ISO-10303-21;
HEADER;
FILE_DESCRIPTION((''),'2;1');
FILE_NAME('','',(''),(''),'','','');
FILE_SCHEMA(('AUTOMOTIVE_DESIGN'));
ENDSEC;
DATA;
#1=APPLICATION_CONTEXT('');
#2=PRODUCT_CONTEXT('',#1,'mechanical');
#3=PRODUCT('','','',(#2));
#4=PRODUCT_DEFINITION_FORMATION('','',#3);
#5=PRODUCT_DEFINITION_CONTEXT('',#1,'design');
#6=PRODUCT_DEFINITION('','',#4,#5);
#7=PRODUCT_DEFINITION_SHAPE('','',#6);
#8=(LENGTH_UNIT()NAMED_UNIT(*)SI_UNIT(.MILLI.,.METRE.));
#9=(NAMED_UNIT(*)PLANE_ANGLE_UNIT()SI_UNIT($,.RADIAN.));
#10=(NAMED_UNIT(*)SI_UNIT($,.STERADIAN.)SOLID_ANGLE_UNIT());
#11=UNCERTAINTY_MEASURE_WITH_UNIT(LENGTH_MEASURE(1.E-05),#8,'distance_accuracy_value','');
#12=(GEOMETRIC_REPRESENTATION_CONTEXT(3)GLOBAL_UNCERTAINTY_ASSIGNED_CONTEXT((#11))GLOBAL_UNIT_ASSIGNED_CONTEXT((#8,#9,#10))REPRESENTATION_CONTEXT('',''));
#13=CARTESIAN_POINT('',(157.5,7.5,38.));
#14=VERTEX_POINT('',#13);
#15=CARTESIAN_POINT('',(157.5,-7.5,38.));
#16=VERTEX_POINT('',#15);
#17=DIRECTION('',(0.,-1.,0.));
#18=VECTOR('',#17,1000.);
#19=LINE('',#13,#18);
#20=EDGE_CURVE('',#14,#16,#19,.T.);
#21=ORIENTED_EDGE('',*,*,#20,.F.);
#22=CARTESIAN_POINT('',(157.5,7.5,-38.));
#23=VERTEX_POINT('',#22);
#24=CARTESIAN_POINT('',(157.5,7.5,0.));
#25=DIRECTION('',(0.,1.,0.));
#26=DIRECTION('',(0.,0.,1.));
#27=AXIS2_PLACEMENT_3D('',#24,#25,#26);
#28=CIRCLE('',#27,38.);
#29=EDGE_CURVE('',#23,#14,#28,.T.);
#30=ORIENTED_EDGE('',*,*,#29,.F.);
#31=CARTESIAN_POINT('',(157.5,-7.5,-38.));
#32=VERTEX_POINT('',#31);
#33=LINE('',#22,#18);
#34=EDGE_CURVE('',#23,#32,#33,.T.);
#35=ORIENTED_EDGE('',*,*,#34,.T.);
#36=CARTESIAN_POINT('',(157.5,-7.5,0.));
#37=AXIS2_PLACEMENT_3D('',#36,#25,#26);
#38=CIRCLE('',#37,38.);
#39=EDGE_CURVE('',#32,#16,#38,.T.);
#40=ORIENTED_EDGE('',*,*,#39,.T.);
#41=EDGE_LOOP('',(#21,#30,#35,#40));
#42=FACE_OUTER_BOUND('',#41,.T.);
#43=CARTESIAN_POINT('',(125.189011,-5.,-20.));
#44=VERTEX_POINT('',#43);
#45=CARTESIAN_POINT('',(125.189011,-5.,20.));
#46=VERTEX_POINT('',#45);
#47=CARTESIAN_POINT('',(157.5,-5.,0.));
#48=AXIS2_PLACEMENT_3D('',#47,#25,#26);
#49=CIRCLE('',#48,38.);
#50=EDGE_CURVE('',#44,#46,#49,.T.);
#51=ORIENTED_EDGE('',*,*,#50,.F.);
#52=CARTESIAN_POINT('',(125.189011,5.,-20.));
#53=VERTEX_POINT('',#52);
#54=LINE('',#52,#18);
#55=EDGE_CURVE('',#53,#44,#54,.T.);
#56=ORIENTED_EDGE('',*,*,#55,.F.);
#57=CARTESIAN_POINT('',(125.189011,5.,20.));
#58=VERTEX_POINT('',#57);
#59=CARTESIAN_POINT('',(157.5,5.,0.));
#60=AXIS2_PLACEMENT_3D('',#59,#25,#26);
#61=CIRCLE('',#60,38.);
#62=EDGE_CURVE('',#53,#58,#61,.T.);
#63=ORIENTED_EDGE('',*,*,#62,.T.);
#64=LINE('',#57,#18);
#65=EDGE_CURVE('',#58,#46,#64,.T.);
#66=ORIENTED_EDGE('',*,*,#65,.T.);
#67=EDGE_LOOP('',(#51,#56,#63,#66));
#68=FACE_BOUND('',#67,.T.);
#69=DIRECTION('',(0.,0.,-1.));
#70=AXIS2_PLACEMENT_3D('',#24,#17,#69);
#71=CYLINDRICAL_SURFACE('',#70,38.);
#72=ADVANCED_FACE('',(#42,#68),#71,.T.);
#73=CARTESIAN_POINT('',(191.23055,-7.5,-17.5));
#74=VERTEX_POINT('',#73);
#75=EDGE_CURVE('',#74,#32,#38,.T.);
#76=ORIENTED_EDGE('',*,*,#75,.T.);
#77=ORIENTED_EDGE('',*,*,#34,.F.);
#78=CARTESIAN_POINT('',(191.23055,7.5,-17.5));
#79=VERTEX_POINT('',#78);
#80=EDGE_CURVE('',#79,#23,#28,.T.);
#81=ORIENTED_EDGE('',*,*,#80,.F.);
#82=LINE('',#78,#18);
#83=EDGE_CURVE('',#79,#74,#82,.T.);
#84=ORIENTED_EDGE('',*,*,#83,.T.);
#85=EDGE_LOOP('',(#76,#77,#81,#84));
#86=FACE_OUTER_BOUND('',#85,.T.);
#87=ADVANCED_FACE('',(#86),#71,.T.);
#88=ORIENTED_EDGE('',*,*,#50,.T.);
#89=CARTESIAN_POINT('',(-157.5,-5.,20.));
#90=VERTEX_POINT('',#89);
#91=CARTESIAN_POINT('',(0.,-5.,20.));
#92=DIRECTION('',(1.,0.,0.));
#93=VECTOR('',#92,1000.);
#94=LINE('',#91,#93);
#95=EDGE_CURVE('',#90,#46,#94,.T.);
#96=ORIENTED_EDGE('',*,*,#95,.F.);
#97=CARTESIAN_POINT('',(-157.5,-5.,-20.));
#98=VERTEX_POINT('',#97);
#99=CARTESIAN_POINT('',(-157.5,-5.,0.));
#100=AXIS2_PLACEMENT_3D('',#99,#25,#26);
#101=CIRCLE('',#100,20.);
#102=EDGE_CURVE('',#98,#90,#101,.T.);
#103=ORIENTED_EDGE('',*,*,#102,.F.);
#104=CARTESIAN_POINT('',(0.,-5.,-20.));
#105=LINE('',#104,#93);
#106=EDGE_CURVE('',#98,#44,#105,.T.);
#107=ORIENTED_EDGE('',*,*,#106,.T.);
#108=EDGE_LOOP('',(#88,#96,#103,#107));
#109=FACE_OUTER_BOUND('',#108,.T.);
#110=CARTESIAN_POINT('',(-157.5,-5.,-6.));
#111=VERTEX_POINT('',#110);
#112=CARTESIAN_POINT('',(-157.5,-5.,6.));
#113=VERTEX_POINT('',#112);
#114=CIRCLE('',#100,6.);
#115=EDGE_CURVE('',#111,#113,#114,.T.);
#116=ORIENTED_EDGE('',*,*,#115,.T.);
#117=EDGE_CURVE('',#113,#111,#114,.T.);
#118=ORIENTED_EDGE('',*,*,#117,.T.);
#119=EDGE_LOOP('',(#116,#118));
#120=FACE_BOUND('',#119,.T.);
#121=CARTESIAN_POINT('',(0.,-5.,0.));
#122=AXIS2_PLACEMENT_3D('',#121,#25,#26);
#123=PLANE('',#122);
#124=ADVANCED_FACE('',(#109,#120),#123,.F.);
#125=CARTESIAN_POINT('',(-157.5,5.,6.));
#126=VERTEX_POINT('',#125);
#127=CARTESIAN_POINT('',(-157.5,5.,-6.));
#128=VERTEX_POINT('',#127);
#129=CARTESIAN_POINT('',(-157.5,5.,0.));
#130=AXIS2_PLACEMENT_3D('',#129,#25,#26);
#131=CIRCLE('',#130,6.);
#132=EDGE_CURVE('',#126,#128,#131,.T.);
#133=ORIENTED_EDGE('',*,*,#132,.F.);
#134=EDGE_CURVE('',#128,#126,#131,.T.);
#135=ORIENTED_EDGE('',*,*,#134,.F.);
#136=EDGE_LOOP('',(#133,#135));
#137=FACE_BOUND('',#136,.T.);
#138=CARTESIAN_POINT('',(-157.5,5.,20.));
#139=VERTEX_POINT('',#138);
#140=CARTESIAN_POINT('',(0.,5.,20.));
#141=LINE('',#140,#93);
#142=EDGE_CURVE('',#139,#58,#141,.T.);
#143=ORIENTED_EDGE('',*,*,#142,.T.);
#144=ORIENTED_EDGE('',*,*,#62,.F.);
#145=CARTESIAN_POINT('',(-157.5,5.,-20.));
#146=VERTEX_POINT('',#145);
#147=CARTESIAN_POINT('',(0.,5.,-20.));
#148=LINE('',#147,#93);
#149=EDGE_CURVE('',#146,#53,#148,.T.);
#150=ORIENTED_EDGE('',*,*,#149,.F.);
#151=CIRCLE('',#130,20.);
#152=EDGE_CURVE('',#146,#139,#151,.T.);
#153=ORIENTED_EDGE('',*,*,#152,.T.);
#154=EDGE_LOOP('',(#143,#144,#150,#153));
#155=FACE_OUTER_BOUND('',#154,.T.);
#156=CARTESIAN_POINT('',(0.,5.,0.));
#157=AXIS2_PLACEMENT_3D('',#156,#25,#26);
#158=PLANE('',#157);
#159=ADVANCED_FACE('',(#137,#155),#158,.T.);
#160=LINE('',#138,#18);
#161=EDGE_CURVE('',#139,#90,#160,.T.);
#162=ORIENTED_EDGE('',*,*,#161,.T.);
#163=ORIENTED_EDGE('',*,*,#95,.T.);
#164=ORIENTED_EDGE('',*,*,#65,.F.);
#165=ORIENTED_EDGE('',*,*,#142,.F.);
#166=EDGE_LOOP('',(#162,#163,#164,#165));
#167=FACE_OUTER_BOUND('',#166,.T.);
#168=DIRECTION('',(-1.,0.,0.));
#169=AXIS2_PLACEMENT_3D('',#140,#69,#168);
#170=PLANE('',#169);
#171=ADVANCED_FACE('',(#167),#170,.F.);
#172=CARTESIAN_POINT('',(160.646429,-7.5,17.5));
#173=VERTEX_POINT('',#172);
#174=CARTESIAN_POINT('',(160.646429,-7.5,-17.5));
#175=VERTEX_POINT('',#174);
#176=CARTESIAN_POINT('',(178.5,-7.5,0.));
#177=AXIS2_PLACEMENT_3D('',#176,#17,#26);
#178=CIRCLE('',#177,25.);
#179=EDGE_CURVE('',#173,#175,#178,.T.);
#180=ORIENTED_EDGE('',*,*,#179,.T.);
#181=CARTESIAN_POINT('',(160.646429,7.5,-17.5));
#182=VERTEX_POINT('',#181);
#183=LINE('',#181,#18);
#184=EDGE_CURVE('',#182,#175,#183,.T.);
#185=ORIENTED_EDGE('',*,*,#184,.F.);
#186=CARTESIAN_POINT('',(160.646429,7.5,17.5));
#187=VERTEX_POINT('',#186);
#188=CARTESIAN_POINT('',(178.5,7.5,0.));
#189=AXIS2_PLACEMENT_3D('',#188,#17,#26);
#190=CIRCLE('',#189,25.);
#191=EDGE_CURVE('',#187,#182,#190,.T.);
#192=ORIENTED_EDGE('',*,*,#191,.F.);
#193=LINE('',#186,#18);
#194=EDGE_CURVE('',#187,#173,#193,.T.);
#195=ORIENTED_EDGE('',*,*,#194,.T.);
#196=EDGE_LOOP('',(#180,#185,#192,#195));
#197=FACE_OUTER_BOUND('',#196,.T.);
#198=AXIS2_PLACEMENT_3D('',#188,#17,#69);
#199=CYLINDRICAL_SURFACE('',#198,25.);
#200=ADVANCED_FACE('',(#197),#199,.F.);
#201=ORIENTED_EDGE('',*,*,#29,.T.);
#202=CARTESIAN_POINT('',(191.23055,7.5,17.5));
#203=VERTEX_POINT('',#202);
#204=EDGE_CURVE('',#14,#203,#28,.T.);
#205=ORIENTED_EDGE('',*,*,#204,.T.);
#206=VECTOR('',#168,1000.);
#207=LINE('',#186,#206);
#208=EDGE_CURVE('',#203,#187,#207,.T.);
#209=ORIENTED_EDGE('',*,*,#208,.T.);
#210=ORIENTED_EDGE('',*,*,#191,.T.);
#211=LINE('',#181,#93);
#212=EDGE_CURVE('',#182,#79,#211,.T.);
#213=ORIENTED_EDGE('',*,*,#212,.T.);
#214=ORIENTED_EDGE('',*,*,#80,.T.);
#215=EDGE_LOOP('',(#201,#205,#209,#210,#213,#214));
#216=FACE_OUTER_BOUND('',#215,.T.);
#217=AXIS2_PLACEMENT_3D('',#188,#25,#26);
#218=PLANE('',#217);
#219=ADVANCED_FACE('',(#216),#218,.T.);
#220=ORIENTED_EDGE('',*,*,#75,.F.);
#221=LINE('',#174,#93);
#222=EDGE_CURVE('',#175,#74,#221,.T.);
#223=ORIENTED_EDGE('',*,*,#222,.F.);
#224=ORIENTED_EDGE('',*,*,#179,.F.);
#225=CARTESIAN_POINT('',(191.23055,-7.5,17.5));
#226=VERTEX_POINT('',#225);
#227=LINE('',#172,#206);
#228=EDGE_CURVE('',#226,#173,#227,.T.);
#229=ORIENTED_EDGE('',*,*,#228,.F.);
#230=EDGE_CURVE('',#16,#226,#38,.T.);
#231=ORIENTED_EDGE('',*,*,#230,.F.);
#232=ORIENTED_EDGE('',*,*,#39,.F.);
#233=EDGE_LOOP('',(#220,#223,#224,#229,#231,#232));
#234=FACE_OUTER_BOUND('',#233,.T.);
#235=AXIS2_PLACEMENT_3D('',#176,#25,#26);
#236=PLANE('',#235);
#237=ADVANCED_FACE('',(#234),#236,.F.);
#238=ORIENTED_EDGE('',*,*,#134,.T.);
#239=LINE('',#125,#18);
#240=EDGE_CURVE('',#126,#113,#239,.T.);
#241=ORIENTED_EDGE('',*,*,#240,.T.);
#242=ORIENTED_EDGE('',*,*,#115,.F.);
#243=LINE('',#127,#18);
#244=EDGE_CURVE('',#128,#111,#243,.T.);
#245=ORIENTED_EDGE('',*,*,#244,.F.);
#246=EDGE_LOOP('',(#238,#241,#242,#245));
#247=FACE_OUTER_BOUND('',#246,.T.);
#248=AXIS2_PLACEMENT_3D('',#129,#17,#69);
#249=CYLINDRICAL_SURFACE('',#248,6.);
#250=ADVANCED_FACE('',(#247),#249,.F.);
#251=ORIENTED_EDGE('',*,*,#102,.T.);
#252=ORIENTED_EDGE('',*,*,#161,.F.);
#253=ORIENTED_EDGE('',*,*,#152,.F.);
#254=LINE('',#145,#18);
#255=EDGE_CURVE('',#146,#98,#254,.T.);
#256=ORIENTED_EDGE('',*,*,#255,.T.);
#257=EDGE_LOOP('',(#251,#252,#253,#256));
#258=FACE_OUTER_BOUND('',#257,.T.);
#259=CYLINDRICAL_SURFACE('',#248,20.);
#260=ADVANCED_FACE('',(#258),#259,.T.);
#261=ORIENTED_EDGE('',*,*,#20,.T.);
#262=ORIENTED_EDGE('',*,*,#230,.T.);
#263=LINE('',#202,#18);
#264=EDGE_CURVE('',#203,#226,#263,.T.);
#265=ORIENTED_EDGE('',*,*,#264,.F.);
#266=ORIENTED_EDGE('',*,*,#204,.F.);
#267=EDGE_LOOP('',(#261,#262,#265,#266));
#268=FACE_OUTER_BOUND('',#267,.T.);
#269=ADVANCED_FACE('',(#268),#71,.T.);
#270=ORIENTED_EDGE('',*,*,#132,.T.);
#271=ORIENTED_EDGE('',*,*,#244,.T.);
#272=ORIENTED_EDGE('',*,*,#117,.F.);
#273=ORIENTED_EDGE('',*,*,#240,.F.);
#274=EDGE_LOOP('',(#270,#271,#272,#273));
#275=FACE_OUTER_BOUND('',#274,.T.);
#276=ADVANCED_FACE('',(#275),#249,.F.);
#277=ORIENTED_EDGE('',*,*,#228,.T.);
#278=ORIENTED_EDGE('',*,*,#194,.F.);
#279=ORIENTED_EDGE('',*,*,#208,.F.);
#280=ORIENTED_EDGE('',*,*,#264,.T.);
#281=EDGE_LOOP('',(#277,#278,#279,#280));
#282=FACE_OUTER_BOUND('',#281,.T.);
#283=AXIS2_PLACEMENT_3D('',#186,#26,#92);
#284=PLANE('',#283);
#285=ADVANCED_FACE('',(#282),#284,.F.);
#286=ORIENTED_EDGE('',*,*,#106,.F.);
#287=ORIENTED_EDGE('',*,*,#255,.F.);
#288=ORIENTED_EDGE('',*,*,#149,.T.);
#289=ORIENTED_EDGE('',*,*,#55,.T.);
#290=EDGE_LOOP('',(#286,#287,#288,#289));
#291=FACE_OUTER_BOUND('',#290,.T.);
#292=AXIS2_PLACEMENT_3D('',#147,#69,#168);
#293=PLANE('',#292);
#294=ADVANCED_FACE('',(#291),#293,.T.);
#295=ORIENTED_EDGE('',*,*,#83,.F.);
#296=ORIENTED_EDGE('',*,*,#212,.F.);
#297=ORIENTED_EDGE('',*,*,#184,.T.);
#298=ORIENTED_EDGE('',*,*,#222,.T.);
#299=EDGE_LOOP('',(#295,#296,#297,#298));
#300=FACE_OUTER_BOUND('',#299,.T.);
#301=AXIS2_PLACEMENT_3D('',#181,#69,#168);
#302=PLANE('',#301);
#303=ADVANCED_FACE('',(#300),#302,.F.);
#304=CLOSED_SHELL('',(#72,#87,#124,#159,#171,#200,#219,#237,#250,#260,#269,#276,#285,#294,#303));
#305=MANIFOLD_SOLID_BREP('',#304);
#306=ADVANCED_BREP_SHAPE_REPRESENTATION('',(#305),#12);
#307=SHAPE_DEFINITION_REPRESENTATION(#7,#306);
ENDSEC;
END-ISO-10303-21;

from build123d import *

# Parameters (mm, degrees)
WRENCH_OUTLINE_SKETCH_R  = 6
WRENCH_HANDLE_10MM_DEPTH = 5
JAW_HEAD_BOSS_15MM_DEPTH = 7.5


with BuildPart() as part:
    # Wrench Outline Sketch → Wrench Handle 10mm (new, symmetric)
    with BuildSketch(Plane(origin=(0, 0, 0), x_dir=(1, 0, 0), z_dir=(0, 1, 0))):
        with BuildLine():
            Line((125.189011157, 20), (-157.5, 20))
            ThreePointArc((-157.5, 20), (-177.5, 0), (-157.5, -20))
            Line((-157.5, -20), (125.189011157, -20))
            ThreePointArc((125.189011157, -20), (119.5, 0), (125.189011157, 20))
        make_face()
        with Locations(Location((-157.5, 0, 0), (0, 0, 270))):
            Circle(WRENCH_OUTLINE_SKETCH_R, mode=Mode.SUBTRACT)
    extrude(amount=WRENCH_HANDLE_10MM_DEPTH, both=True)

    # Jaw Head Sketch → Jaw Head Boss 15mm (add, symmetric)
    with BuildSketch(Plane(origin=(0, 0, 0), x_dir=(1, 0, 0), z_dir=(0, 1, 0))):
        with BuildLine():
            Line((160.646428929, -17.5), (191.230549951, -17.5))
            ThreePointArc((191.230549951, -17.5), (119.5, 0), (191.230549951, 17.5))
            Line((191.230549951, 17.5), (160.646428929, 17.5))
            ThreePointArc((160.646428929, 17.5), (153.5, 0), (160.646428929, -17.5))
        make_face()
    extrude(amount=JAW_HEAD_BOSS_15MM_DEPTH, both=True)


solid = part.part
